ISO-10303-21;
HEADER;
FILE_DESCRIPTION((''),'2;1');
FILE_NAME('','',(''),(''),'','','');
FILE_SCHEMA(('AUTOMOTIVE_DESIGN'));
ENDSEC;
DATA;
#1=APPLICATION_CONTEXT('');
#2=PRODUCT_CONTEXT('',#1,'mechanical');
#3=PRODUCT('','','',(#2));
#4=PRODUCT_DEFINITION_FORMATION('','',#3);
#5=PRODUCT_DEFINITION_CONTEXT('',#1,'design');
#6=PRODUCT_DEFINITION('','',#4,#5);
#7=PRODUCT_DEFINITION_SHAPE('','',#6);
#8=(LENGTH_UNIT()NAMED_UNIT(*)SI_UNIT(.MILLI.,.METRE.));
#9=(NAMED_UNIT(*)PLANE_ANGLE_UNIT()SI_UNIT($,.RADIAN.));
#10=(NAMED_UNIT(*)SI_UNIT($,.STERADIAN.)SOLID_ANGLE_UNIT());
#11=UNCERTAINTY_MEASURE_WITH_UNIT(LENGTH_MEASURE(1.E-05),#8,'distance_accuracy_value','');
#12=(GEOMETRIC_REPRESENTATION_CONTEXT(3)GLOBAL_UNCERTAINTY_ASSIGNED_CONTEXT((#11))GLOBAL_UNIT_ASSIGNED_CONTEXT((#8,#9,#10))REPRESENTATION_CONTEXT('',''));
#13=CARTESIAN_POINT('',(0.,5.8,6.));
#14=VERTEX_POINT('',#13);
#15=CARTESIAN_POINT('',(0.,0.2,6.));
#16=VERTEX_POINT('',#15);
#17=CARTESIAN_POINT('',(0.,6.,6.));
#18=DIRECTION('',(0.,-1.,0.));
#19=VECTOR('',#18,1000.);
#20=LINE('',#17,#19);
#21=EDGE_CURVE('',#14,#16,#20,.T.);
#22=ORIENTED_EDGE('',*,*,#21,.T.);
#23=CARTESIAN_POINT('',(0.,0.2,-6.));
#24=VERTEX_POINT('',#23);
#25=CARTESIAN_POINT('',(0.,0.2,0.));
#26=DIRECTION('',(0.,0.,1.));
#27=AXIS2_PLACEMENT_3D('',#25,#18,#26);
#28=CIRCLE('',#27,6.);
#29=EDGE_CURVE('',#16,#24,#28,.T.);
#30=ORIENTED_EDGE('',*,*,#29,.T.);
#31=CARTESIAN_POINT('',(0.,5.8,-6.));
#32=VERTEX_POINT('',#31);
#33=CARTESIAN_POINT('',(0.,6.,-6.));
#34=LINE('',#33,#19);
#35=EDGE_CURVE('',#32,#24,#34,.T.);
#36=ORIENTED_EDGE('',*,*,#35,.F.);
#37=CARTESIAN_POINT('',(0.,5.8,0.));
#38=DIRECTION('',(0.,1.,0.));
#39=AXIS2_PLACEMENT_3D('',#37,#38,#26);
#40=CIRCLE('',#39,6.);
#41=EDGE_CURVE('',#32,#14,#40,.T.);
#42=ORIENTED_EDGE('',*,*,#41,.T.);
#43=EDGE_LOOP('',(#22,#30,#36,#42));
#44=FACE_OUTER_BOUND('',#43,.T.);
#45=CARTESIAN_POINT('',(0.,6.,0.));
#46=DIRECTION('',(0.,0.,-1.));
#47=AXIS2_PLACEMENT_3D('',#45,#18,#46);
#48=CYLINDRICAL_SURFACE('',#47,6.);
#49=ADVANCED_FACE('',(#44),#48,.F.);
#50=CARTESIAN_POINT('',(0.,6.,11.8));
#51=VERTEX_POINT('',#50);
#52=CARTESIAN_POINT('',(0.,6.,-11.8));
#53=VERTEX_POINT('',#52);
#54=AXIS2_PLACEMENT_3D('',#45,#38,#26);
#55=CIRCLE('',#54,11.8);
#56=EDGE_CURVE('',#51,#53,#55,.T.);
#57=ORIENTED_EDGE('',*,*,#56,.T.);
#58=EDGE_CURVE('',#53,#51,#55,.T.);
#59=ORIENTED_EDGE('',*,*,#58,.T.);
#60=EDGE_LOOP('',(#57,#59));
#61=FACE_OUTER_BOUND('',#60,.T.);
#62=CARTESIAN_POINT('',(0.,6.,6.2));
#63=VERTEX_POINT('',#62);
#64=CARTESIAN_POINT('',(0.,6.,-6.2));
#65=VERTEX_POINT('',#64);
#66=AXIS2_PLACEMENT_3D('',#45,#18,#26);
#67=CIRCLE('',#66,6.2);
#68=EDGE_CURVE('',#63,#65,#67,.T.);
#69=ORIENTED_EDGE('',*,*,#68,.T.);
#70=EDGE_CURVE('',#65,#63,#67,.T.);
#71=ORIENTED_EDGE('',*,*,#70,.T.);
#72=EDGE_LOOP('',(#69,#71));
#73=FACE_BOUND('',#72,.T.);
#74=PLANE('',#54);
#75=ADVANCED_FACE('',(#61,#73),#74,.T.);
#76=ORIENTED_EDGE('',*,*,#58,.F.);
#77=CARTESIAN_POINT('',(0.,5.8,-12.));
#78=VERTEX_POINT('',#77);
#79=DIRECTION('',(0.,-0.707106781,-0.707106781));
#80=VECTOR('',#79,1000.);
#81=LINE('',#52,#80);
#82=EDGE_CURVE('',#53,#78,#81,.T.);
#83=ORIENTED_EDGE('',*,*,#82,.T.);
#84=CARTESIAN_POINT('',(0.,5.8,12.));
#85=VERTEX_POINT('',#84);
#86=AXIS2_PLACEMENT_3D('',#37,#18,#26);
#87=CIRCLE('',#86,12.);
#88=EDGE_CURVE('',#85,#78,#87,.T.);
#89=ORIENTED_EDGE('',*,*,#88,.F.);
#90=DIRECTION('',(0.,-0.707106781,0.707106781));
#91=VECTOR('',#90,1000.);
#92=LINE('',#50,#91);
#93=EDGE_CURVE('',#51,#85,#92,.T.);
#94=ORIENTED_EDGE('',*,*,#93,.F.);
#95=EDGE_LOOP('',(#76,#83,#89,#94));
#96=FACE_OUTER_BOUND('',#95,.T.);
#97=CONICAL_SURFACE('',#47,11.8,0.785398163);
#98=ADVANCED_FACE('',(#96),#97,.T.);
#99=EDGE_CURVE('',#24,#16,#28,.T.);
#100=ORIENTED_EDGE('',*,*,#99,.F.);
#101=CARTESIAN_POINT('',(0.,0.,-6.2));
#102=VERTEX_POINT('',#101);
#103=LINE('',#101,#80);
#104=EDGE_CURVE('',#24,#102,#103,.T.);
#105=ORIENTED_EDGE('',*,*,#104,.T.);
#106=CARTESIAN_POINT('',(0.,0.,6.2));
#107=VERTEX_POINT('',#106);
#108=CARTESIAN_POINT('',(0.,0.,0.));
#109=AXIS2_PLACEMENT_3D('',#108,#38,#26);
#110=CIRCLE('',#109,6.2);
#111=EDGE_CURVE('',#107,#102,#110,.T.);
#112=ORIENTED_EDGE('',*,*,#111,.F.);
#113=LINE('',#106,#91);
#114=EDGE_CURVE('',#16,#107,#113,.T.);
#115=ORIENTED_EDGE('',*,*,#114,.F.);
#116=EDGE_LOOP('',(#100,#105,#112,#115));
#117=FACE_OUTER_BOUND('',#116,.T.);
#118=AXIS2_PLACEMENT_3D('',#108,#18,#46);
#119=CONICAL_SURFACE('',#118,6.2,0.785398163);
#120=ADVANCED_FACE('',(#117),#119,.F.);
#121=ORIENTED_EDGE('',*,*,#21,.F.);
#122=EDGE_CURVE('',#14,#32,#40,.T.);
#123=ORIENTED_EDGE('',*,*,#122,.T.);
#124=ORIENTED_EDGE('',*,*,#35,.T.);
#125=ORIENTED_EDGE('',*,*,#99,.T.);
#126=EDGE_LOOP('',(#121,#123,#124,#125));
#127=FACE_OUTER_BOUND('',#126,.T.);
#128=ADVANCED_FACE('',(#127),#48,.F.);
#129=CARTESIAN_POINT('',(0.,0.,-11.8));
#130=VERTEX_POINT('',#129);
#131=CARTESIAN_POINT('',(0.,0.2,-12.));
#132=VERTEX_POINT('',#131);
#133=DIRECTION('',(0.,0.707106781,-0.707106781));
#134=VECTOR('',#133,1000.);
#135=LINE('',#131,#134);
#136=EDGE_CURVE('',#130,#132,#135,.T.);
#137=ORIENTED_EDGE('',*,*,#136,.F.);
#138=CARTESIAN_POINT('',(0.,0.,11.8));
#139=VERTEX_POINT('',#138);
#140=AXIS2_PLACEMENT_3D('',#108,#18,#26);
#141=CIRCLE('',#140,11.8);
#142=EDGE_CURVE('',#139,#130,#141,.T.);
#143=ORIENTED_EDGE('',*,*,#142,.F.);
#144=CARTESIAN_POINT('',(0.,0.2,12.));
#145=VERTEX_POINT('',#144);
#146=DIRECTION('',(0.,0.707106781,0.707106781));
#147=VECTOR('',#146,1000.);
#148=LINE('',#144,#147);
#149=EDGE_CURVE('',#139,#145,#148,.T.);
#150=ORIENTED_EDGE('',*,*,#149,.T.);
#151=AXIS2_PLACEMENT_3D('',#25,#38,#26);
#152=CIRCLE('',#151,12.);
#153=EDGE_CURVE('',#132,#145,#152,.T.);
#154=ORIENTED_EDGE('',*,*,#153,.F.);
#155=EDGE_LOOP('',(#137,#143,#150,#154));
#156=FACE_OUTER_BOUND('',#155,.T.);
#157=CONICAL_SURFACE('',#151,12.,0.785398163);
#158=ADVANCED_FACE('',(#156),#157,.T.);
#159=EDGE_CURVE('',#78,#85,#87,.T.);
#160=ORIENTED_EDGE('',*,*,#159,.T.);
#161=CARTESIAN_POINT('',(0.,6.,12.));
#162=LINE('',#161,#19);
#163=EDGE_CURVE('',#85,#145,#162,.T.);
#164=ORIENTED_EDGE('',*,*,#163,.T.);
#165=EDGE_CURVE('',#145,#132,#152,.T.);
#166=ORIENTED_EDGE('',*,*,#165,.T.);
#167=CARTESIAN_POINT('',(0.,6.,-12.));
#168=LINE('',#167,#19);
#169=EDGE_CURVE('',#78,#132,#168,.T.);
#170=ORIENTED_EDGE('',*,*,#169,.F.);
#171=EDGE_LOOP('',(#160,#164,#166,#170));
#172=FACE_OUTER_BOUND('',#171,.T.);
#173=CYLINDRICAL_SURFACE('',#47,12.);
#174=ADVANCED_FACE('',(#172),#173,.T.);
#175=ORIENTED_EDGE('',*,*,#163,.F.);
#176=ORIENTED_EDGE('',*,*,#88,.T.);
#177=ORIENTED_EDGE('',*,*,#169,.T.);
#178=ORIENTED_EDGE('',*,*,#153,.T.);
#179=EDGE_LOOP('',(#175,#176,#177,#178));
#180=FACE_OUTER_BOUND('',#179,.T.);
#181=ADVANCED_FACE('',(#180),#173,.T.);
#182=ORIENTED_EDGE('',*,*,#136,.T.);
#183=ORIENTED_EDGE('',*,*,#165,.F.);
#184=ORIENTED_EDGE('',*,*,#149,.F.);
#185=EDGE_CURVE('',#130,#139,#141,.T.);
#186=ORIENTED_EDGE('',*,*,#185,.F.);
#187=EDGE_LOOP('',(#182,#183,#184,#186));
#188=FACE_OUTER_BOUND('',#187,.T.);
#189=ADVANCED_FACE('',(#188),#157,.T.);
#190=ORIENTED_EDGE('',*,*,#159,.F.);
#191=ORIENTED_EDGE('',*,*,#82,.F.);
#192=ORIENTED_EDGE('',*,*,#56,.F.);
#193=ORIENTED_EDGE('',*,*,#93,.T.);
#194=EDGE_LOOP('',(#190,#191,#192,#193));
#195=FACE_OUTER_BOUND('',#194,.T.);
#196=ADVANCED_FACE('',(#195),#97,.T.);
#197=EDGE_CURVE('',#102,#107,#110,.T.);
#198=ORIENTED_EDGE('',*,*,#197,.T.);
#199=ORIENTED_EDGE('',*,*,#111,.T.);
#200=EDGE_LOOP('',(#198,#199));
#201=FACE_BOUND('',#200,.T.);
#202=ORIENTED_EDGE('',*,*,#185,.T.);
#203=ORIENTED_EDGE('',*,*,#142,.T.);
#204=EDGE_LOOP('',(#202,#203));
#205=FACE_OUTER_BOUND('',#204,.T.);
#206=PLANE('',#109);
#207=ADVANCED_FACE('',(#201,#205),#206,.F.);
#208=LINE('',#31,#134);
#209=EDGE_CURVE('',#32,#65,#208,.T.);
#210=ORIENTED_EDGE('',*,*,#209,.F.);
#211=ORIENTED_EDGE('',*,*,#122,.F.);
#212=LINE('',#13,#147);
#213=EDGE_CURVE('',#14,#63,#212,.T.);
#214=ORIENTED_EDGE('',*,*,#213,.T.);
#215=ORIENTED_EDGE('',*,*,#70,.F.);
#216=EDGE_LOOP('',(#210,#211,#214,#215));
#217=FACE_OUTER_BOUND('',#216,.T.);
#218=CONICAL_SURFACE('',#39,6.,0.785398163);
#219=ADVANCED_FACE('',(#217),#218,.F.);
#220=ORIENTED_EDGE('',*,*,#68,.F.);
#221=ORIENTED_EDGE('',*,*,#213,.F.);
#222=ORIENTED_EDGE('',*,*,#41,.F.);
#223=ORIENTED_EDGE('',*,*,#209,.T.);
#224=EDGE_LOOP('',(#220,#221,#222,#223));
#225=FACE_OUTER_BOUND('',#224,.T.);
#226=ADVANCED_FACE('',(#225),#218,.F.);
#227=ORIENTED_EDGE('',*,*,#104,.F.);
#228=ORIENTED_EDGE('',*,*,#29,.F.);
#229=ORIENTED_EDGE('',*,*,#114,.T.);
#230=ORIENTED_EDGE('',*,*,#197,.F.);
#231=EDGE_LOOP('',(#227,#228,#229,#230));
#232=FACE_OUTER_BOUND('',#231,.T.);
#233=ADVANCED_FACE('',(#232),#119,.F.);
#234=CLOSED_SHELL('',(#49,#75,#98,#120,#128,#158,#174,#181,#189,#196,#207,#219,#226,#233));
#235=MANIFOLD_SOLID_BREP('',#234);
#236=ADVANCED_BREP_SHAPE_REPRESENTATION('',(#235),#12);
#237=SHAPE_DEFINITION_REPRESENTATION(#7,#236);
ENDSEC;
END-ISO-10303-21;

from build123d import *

# Parameters (mm, degrees)
SKETCH_1_R      = 12
SKETCH_1_R_2    = 6
EXTRUDE_1_DEPTH = 6
CHAMFER_1_SIZE  = 0.2


with BuildPart() as part:
    # 草图1 → 拉伸1 (new body)
    with BuildSketch(Plane(origin=(0, 0, 0), x_dir=(1, 0, 0), z_dir=(0, 1, 0))):
        with Locations(Location((0, 0, 0), (0, 0, 270))):
            Circle(SKETCH_1_R)
        with Locations(Location((0, 0, 0), (0, 0, 270))):
            Circle(SKETCH_1_R_2, mode=Mode.SUBTRACT)
    extrude(amount=EXTRUDE_1_DEPTH)

    # 倒角1
    chamfer_1_edges = [part.edges().sort_by_distance(p)[0] for p in [
        (0, 0, -12),
        (0, 6, -12),
        (0, 0, -6),
        (0, 6, -6),
    ]]
    chamfer(chamfer_1_edges, length=CHAMFER_1_SIZE)


solid = part.part
